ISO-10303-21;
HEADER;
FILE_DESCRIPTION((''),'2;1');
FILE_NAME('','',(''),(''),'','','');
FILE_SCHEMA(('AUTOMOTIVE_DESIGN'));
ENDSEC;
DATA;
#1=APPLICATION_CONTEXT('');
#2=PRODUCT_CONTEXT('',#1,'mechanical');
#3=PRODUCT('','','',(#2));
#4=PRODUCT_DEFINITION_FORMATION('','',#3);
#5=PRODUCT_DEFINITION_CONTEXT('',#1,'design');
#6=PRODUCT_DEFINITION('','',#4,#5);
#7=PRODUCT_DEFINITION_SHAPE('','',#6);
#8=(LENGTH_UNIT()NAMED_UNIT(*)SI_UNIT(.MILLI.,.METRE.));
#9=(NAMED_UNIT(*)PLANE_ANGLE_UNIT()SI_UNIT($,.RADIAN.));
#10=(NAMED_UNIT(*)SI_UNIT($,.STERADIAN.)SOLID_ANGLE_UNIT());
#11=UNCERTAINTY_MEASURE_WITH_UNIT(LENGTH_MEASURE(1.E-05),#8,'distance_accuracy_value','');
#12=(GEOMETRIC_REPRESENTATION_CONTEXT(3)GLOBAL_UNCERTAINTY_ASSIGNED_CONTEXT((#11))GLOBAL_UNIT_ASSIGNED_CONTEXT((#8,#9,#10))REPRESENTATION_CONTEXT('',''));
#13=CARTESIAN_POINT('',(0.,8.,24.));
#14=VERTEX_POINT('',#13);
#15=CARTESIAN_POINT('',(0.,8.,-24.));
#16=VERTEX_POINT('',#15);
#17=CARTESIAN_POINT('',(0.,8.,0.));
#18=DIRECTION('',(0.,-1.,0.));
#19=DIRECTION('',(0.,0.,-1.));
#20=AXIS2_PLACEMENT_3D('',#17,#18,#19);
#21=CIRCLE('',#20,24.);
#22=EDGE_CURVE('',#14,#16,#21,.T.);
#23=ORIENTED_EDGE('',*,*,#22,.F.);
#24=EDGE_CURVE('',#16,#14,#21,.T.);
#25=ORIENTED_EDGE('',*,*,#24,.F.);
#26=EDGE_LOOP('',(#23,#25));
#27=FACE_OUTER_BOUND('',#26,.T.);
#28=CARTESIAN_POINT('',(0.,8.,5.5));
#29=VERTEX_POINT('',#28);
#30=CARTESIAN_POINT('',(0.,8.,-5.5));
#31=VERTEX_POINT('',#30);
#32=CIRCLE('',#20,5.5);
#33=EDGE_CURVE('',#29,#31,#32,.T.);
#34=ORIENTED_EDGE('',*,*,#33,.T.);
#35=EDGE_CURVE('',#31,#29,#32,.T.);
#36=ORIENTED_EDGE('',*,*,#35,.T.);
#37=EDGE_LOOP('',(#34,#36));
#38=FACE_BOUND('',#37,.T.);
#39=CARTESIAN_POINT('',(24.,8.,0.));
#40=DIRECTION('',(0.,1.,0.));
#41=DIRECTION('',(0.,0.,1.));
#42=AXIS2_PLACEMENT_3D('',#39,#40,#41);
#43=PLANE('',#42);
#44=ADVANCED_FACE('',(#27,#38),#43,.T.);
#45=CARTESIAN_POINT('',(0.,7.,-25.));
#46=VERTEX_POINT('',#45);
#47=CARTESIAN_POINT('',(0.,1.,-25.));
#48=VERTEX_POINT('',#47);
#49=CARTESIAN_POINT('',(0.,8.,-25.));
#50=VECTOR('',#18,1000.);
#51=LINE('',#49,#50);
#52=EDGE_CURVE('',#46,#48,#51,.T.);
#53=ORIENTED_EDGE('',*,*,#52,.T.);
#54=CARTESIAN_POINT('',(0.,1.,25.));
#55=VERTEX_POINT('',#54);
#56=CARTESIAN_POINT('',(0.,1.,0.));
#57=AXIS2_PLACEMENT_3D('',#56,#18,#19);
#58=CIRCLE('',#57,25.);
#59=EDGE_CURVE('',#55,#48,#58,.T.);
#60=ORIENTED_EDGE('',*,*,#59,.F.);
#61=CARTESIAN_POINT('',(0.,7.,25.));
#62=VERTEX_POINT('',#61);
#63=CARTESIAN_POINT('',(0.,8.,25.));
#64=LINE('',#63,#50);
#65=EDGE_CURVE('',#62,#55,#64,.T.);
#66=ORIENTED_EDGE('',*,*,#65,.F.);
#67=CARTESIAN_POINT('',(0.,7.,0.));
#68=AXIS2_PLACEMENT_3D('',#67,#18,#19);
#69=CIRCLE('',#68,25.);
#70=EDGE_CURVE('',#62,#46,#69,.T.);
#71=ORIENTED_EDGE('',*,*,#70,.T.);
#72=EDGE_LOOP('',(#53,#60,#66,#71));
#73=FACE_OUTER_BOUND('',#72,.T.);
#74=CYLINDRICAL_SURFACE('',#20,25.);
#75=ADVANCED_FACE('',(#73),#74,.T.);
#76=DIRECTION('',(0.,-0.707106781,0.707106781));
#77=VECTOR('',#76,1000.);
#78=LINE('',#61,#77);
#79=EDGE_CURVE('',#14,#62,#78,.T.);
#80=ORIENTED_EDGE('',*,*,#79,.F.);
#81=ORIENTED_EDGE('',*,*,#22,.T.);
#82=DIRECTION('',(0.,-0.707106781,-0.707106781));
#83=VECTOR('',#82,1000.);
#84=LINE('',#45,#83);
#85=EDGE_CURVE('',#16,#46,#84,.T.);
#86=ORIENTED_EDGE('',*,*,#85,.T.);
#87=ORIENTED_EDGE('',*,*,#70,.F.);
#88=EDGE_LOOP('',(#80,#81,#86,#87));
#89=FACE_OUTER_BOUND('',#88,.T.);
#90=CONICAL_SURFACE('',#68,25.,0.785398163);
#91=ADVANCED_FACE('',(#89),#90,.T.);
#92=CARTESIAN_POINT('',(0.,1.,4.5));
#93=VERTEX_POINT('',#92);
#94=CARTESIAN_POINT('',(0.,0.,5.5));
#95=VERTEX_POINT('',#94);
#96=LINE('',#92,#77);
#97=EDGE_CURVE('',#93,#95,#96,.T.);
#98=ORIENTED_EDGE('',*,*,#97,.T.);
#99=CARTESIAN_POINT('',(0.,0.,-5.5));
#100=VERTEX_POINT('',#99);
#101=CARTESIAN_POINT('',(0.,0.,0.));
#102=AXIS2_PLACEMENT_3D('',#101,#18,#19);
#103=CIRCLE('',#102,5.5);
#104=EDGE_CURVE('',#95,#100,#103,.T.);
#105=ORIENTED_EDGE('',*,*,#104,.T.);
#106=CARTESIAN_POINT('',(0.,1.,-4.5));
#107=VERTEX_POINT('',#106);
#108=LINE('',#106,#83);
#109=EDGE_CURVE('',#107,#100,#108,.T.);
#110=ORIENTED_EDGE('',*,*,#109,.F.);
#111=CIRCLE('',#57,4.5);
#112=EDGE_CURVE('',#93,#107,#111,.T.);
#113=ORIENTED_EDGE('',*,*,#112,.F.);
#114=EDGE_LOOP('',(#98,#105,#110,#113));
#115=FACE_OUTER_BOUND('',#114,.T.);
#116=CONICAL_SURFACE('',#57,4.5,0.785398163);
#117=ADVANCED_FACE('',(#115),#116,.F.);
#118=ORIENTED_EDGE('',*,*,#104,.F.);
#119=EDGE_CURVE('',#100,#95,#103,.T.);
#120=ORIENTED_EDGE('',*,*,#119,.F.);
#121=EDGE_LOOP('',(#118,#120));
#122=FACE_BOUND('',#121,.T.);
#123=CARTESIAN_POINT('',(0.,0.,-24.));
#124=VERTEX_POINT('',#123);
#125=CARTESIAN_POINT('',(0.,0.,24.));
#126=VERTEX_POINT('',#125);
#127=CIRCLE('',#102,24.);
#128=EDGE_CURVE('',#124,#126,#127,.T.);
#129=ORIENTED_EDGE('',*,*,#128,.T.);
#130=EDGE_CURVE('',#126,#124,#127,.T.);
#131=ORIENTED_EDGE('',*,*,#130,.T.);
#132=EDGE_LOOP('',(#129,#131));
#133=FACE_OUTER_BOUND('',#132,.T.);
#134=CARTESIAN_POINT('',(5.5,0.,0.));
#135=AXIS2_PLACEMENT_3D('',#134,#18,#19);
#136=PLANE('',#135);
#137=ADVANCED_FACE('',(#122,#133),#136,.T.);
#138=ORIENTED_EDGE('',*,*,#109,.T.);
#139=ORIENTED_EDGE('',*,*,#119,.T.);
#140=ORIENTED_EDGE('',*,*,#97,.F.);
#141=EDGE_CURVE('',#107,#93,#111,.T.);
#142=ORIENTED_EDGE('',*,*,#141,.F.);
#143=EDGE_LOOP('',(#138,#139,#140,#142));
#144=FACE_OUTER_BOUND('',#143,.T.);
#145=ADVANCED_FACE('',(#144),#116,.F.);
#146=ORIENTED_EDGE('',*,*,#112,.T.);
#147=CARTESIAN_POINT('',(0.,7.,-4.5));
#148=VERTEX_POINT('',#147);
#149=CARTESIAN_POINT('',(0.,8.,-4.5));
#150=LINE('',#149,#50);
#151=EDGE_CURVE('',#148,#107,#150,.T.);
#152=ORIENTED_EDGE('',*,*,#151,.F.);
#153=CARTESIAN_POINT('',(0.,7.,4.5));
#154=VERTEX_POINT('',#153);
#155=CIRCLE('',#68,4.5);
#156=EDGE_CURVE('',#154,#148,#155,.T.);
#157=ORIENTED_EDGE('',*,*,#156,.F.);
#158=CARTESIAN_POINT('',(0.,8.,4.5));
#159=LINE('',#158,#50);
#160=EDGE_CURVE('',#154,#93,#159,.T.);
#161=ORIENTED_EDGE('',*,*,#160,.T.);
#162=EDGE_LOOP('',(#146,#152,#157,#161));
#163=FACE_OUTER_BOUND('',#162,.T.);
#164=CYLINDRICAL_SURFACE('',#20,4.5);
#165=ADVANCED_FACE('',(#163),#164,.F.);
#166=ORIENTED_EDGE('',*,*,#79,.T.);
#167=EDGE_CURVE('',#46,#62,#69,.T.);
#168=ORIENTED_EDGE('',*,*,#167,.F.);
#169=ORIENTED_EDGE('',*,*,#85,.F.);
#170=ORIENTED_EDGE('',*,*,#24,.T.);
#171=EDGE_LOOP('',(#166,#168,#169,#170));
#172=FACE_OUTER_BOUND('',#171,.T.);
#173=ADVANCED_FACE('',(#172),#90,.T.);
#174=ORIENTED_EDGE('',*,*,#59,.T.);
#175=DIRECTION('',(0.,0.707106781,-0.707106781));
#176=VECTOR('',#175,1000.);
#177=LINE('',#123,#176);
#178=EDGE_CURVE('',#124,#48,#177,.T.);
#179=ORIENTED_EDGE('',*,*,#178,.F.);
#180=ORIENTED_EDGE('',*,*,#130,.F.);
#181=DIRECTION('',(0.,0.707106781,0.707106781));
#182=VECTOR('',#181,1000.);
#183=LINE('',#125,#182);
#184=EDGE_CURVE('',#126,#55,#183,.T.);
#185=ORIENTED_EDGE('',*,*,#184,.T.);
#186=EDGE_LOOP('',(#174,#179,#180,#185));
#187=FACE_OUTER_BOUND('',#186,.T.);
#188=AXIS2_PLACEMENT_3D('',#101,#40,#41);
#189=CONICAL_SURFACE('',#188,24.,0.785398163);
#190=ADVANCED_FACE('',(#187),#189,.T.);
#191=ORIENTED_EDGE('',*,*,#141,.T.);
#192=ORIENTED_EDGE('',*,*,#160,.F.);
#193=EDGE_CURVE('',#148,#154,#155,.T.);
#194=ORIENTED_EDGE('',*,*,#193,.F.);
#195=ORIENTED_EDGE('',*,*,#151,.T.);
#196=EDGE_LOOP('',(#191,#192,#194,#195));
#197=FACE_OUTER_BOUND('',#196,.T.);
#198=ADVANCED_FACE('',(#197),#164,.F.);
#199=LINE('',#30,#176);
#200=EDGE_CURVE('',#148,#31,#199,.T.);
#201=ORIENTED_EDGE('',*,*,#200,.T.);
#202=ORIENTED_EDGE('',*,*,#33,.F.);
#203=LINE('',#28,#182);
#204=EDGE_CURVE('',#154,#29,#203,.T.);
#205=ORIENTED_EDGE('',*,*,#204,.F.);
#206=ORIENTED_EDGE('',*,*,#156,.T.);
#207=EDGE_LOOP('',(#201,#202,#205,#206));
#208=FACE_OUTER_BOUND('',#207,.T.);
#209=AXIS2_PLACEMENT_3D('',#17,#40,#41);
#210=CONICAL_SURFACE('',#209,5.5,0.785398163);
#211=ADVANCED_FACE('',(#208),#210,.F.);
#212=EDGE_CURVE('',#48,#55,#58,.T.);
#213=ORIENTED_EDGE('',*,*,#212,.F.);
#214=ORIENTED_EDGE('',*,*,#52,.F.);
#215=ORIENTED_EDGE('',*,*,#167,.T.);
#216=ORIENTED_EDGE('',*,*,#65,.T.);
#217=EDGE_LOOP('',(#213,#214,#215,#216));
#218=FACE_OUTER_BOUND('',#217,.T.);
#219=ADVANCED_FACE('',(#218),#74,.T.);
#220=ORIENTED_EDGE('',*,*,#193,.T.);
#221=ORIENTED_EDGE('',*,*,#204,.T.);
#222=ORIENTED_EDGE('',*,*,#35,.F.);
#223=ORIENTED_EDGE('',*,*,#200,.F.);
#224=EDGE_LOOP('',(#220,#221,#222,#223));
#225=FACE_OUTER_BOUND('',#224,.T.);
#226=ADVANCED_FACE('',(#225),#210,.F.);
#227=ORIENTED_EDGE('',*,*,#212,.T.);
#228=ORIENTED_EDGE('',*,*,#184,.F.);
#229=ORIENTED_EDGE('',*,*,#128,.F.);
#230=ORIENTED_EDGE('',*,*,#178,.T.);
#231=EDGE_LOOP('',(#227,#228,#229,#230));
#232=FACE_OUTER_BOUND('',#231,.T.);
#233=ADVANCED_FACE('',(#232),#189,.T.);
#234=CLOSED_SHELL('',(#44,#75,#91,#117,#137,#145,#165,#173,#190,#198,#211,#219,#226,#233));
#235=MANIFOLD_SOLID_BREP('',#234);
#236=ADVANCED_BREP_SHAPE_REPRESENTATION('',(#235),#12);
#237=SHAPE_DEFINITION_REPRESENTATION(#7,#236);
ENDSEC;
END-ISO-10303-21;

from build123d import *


with BuildPart() as part:
    # 草图1 → 旋转1 (revolve)
    with BuildSketch(Plane.XY, mode=Mode.PRIVATE) as revolve_1_sk:
        Polygon((24, 8), (5.5, 8), (4.5, 7), (4.5, 1), (5.5, 0), (24, 0), (25, 1), (25, 7), align=None)
    revolve(revolve_1_sk.sketch.rotate(Axis((0, 8, 0), (0, -1, 0)), 270), axis=Axis((0, 8, 0), (0, -1, 0)))


solid = part.part
